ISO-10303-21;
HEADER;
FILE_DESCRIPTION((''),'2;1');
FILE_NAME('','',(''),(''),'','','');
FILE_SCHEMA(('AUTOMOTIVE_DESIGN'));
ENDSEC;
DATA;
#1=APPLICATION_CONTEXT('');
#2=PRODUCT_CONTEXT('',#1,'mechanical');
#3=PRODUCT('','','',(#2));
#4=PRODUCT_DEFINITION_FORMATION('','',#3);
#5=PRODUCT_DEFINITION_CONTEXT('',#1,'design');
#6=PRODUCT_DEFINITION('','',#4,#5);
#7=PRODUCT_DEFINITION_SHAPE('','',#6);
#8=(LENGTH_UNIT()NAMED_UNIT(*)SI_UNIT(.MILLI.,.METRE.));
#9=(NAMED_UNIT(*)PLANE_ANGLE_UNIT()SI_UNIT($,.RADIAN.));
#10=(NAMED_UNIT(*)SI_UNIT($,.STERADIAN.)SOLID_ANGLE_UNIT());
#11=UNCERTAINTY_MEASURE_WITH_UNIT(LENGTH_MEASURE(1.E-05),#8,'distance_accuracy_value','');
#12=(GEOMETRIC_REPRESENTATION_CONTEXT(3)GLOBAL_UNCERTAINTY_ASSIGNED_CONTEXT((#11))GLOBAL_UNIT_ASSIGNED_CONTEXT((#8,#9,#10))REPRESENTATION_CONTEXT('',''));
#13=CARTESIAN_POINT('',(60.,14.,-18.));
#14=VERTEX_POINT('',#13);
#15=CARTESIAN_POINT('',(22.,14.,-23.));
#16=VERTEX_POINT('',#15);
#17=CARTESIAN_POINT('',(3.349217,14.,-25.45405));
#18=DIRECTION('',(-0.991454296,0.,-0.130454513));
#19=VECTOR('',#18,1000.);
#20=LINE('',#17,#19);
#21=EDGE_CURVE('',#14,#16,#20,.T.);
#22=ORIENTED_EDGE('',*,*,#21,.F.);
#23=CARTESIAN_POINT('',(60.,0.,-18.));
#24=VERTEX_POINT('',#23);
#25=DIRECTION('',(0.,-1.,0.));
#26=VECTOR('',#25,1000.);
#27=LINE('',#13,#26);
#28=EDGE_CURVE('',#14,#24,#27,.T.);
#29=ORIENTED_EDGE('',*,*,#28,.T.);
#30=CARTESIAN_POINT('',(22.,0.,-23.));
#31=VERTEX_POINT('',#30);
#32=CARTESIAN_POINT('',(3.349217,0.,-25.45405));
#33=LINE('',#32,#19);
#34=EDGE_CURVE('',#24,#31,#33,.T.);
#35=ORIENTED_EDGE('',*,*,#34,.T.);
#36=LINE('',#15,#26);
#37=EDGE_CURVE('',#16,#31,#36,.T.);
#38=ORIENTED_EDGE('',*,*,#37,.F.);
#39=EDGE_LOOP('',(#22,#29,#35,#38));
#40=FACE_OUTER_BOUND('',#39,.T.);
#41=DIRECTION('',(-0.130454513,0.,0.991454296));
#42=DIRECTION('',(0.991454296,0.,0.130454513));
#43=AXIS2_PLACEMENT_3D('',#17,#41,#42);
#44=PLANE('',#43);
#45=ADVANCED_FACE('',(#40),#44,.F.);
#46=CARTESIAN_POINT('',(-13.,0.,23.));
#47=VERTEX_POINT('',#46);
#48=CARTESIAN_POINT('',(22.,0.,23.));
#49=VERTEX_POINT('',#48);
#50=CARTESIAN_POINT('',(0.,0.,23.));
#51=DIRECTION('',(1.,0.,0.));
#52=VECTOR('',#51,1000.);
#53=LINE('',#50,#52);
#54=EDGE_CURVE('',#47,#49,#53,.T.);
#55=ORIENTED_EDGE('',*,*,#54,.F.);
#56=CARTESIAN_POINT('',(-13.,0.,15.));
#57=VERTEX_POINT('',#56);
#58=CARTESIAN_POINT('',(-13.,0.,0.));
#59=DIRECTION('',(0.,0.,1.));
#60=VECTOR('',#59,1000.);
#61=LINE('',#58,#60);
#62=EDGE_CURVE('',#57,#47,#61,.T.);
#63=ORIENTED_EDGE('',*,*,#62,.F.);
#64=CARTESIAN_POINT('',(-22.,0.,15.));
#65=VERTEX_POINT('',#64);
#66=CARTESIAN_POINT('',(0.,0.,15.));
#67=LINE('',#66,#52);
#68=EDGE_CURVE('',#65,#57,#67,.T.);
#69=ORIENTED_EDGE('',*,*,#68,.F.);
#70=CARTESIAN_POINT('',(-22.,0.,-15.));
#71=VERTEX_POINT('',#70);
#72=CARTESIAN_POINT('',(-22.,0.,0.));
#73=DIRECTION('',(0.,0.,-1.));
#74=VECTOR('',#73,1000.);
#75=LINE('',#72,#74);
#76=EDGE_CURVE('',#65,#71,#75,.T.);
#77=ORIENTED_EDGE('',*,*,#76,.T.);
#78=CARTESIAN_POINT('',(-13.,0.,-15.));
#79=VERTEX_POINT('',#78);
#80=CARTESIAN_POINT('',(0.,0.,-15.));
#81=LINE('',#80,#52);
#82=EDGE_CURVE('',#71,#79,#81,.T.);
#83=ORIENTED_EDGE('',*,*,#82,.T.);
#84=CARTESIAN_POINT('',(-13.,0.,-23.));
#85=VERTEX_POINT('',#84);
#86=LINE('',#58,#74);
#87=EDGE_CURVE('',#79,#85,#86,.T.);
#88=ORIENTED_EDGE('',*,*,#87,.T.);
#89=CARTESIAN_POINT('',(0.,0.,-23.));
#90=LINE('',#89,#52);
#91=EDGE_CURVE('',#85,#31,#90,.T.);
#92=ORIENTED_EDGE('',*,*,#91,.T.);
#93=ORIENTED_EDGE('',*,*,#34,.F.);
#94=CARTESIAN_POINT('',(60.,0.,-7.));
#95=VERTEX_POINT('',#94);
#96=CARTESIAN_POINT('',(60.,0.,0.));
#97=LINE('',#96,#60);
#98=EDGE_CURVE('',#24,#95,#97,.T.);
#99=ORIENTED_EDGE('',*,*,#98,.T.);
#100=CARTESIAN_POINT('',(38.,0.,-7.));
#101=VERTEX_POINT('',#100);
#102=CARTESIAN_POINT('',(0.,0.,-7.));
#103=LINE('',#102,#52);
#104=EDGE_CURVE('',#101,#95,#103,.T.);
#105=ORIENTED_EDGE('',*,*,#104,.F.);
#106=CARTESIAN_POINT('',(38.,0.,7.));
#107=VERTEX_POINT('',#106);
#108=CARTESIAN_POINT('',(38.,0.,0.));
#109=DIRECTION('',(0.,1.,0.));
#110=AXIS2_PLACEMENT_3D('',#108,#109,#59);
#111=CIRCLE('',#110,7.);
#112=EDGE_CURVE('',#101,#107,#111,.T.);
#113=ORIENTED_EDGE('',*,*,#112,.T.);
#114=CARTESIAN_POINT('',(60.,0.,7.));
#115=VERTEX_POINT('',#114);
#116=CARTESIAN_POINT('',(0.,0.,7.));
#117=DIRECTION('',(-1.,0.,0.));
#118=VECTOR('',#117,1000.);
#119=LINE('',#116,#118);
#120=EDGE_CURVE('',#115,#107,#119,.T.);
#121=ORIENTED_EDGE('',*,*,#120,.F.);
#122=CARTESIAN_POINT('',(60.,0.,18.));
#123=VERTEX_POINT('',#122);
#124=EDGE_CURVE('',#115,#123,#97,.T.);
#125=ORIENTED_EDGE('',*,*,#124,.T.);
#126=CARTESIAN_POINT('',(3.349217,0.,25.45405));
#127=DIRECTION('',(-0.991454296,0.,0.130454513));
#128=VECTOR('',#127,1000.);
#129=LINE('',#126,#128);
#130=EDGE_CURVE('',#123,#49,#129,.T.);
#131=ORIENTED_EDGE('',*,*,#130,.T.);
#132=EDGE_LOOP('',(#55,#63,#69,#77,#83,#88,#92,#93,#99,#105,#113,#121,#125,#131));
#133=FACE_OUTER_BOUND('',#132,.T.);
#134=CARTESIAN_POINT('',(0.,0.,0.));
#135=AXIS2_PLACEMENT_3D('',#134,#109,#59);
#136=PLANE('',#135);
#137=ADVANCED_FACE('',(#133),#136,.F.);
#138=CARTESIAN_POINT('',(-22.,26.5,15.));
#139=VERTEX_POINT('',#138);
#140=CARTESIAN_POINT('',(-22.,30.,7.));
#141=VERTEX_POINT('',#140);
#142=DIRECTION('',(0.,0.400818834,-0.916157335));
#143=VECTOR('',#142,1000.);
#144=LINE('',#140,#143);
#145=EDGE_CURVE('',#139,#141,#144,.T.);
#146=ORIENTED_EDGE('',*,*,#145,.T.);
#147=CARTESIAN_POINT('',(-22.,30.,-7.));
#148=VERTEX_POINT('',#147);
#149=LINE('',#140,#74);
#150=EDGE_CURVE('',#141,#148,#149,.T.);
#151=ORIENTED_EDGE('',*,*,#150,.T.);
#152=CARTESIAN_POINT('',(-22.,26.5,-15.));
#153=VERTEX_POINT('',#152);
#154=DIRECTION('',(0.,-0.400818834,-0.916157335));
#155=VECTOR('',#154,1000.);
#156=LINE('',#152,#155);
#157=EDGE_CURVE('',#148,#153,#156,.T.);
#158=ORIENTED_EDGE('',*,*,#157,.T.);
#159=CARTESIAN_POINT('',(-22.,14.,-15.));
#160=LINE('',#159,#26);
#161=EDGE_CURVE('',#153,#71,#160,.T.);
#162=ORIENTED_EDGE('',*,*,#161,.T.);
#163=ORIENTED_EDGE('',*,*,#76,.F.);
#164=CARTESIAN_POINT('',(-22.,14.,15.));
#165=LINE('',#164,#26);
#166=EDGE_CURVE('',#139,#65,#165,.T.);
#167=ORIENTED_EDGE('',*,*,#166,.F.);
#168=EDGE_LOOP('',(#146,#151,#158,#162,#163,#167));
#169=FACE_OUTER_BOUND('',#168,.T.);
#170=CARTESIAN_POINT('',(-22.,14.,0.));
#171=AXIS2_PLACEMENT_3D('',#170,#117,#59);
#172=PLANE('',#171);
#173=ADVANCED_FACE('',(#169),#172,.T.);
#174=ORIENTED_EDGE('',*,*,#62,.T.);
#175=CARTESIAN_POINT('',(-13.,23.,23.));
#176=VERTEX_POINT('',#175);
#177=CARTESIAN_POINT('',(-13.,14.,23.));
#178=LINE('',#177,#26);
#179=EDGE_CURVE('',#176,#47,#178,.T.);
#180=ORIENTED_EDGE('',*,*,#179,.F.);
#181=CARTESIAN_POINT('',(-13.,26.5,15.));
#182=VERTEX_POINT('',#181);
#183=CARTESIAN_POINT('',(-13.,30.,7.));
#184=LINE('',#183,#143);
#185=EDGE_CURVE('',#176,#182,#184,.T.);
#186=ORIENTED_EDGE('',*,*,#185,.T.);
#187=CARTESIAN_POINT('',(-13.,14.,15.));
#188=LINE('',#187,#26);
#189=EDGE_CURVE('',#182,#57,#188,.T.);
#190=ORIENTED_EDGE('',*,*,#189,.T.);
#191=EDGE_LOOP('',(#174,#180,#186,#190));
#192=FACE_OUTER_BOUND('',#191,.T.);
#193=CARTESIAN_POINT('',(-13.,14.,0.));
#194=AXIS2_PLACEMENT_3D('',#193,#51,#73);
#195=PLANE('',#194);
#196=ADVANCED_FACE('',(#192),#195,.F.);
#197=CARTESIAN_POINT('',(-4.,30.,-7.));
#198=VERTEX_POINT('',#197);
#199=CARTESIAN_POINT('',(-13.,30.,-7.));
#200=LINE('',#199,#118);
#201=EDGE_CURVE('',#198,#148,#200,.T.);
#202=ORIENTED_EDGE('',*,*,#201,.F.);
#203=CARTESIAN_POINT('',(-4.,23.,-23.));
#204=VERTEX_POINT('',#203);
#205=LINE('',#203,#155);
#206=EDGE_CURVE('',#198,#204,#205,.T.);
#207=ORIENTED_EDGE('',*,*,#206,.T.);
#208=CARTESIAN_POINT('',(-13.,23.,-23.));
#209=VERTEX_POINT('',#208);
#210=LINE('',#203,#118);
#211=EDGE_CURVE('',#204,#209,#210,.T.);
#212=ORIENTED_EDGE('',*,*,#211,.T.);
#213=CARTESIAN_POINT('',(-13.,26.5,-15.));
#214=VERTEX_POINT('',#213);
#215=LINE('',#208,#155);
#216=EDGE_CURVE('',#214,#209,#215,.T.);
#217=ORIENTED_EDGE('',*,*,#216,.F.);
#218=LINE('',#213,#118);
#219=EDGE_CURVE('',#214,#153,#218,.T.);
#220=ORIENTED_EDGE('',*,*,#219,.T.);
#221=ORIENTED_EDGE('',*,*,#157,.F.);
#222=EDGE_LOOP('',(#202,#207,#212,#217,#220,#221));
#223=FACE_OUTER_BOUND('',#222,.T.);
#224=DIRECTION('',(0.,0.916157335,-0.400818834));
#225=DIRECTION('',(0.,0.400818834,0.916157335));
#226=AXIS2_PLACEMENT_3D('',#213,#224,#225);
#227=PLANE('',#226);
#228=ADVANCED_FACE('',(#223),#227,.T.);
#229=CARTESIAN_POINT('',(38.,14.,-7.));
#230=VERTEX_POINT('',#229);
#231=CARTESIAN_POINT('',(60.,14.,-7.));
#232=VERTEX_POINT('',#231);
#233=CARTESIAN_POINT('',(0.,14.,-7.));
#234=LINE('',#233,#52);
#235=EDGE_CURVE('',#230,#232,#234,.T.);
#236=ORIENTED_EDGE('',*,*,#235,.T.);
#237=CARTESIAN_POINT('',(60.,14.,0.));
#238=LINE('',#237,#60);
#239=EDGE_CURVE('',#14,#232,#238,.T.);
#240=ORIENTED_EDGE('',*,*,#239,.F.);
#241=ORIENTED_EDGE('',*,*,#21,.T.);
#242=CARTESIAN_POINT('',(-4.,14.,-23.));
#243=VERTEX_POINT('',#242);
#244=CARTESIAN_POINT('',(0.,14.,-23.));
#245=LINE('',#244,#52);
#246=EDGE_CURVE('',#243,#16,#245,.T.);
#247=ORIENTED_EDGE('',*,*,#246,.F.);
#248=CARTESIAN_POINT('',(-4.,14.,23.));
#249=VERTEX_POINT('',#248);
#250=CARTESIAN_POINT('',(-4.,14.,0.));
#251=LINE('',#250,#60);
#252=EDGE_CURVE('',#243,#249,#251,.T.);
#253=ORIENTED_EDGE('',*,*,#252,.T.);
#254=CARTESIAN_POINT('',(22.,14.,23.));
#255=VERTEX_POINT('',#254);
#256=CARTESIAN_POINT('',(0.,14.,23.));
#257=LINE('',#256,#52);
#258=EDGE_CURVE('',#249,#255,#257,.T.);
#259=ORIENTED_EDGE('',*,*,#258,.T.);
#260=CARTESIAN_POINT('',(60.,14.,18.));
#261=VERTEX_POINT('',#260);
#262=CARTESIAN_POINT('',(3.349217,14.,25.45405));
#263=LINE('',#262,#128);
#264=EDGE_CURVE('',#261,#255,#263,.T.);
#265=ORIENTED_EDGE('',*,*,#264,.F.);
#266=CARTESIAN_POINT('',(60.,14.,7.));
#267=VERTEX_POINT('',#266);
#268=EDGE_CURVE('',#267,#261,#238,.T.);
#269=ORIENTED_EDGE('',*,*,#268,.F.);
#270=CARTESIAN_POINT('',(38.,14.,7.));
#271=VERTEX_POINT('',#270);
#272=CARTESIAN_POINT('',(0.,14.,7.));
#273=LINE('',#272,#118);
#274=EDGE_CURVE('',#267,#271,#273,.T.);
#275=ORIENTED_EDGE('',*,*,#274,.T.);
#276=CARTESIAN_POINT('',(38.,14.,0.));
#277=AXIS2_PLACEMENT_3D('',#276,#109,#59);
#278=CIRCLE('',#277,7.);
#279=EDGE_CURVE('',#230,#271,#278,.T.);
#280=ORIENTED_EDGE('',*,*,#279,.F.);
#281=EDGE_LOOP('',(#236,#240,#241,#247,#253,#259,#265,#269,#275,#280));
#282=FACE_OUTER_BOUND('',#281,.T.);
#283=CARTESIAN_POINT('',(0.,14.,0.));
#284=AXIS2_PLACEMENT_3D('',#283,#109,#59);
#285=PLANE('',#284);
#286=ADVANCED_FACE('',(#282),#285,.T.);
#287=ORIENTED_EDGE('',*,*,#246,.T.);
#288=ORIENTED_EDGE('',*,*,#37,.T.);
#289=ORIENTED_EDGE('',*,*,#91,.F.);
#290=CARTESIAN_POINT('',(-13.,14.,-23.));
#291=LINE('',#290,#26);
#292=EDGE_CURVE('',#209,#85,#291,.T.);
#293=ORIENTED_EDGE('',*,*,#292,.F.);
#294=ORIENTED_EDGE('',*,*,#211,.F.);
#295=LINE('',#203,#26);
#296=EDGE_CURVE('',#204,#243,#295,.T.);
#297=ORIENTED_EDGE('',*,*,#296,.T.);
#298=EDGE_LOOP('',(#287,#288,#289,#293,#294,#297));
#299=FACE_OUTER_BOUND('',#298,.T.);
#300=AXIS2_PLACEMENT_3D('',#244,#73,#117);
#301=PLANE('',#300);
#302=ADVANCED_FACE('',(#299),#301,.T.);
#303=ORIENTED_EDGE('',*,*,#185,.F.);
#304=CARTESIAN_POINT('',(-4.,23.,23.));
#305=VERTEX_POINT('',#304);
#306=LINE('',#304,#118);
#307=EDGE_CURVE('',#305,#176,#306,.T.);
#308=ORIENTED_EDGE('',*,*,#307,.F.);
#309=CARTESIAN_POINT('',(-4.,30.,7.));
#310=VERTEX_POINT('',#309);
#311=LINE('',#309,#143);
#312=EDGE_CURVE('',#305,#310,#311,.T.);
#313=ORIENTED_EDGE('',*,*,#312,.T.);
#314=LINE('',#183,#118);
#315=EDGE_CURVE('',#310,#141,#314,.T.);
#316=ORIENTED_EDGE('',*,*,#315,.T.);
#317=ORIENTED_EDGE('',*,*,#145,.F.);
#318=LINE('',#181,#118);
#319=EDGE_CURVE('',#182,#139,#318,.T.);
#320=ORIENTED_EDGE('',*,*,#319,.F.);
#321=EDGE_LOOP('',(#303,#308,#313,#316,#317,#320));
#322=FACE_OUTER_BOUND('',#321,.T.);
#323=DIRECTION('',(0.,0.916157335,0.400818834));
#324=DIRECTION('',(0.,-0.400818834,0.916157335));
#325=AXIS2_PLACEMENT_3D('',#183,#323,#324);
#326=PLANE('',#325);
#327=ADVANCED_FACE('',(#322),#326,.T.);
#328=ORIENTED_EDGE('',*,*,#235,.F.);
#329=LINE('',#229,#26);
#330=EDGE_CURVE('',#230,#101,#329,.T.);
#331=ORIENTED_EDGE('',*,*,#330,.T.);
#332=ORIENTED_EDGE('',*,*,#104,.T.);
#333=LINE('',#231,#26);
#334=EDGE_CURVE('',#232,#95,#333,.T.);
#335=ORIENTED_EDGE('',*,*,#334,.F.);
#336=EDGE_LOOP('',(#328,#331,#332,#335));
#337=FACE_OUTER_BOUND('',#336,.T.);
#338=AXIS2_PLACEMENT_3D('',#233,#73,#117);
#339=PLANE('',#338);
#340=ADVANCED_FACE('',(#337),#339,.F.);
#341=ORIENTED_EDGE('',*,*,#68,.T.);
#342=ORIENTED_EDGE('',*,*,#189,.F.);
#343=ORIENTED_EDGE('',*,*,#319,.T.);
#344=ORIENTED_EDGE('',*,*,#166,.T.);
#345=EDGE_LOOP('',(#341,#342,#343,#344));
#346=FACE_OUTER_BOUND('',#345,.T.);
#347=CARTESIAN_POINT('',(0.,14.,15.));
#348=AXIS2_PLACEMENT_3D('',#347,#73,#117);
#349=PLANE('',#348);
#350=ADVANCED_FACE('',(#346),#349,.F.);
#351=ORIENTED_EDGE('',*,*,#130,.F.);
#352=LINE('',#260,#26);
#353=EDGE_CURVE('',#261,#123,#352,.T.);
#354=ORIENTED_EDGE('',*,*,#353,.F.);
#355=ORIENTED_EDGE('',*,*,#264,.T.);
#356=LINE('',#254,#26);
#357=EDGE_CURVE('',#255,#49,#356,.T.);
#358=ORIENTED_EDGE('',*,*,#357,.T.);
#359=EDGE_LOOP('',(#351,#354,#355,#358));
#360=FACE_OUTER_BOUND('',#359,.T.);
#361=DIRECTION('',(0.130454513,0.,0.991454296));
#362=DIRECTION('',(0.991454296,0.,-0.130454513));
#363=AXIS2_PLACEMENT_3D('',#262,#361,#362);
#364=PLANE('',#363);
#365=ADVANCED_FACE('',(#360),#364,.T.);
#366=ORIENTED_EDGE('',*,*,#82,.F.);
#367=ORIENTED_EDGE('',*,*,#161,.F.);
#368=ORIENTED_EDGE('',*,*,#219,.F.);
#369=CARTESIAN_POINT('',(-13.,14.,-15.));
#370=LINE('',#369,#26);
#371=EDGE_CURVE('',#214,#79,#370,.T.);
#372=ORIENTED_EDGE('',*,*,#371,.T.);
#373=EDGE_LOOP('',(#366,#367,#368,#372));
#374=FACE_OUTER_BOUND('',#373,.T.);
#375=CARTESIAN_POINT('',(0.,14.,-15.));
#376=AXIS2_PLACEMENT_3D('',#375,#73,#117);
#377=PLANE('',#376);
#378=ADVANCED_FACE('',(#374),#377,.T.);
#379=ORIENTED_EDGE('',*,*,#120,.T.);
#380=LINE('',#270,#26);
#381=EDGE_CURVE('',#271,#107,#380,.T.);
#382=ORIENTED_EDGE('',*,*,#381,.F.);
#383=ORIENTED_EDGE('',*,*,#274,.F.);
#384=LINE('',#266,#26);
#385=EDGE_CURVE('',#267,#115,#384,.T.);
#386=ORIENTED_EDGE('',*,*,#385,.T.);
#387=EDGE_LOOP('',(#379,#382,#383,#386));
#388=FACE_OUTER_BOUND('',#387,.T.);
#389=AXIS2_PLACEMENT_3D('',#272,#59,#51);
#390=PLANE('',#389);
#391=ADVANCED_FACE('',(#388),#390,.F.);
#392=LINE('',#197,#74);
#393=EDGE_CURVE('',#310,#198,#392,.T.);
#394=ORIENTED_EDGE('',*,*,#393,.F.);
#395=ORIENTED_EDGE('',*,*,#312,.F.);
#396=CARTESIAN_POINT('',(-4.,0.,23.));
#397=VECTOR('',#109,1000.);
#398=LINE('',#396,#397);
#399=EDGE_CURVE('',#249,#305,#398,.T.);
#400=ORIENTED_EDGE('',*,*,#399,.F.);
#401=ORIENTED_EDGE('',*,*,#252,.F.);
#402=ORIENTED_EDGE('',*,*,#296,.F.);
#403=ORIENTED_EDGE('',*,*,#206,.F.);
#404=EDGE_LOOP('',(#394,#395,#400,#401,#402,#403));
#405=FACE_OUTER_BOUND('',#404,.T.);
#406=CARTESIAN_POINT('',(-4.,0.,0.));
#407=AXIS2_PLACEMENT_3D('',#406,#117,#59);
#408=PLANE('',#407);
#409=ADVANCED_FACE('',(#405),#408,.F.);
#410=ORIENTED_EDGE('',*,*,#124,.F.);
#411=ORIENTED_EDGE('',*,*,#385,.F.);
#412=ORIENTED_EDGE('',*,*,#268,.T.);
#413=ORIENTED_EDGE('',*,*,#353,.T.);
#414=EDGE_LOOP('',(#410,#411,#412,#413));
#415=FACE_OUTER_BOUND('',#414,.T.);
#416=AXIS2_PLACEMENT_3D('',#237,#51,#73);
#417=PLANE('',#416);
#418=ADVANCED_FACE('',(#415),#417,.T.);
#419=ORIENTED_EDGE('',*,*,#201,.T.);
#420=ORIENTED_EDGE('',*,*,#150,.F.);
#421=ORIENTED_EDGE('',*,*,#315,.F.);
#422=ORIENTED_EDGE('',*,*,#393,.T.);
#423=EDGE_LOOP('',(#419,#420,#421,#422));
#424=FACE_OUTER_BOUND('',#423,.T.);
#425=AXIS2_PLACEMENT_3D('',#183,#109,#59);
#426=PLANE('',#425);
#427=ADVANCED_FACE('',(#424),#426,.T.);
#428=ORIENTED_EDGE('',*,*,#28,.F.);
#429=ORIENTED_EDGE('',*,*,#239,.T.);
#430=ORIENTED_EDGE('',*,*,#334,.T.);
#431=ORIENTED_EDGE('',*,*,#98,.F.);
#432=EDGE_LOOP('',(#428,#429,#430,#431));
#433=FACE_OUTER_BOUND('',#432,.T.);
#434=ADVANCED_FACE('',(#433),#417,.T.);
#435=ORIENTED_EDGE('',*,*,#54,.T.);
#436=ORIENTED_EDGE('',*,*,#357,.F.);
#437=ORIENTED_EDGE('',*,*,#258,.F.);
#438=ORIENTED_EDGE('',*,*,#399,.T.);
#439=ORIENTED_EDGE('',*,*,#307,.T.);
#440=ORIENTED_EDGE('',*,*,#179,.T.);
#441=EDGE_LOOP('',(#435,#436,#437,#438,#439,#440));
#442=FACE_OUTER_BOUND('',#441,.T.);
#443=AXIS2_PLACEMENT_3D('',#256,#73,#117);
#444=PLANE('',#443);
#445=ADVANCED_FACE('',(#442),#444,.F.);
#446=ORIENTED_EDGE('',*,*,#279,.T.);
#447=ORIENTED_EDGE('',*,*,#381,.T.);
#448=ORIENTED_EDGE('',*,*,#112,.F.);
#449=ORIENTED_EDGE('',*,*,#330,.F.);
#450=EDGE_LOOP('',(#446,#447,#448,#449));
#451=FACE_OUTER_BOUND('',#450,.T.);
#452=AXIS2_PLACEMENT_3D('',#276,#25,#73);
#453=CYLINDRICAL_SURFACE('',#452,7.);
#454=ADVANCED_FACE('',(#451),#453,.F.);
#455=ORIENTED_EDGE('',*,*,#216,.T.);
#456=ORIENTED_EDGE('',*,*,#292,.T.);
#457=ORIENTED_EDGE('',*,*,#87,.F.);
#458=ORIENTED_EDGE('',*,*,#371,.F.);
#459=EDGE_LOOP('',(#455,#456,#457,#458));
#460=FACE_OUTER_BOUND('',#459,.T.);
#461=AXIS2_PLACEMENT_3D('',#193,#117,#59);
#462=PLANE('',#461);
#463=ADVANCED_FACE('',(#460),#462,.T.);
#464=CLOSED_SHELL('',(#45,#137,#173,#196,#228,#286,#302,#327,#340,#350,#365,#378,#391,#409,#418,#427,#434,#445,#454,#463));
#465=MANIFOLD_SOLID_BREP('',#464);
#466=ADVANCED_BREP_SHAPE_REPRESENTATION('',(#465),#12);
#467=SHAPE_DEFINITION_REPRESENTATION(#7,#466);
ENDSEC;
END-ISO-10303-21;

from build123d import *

# Parameters (mm, degrees)
SLOTTED_BASE_PLATE_DEPTH = 14
UPRIGHT_BLOCK_DEPTH      = 9
TOP_STEP_BOSS_DEPTH      = 9


with BuildPart() as part:
    # Base Plate Profile Sketch → Slotted Base Plate (new body)
    with BuildSketch(Plane(origin=(0, 0, 0), x_dir=(1, 0, 0), z_dir=(0, 1, 0))):
        Polygon((-22, -15), (-13, -15), (-13, -23), (22, -23), (22, 23), (-13, 23), (-13, 15), (-22, 15), align=None)
        with BuildLine():
            ThreePointArc((38, 7), (31, 0), (38, -7))
            Line((38, -7), (60, -7))
            Line((60, -7), (60, -18))
            Line((60, -18), (22, -23))
            Line((22, -23), (22, 23))
            Line((22, 23), (60, 18))
            Line((60, 18), (60, 7))
            Line((60, 7), (38, 7))
        make_face()
    extrude(amount=SLOTTED_BASE_PLATE_DEPTH)

    # Upright Block Sketch → Upright Block (add)
    with BuildSketch(Plane.ZY.offset(22)):
        Polygon((7, 30), (-7, 30), (-15, 26.5), (-15, 0), (15, 0), (15, 26.5), align=None)
    extrude(amount=-UPRIGHT_BLOCK_DEPTH)

    # Top Step Sketch → Top Step Boss (add)
    with BuildSketch(Plane.ZY.offset(13)):
        Polygon((-7, 30), (7, 30), (23, 23), (23, 0), (-23, 0), (-23, 23), align=None)
    extrude(amount=-TOP_STEP_BOSS_DEPTH)


solid = part.part
